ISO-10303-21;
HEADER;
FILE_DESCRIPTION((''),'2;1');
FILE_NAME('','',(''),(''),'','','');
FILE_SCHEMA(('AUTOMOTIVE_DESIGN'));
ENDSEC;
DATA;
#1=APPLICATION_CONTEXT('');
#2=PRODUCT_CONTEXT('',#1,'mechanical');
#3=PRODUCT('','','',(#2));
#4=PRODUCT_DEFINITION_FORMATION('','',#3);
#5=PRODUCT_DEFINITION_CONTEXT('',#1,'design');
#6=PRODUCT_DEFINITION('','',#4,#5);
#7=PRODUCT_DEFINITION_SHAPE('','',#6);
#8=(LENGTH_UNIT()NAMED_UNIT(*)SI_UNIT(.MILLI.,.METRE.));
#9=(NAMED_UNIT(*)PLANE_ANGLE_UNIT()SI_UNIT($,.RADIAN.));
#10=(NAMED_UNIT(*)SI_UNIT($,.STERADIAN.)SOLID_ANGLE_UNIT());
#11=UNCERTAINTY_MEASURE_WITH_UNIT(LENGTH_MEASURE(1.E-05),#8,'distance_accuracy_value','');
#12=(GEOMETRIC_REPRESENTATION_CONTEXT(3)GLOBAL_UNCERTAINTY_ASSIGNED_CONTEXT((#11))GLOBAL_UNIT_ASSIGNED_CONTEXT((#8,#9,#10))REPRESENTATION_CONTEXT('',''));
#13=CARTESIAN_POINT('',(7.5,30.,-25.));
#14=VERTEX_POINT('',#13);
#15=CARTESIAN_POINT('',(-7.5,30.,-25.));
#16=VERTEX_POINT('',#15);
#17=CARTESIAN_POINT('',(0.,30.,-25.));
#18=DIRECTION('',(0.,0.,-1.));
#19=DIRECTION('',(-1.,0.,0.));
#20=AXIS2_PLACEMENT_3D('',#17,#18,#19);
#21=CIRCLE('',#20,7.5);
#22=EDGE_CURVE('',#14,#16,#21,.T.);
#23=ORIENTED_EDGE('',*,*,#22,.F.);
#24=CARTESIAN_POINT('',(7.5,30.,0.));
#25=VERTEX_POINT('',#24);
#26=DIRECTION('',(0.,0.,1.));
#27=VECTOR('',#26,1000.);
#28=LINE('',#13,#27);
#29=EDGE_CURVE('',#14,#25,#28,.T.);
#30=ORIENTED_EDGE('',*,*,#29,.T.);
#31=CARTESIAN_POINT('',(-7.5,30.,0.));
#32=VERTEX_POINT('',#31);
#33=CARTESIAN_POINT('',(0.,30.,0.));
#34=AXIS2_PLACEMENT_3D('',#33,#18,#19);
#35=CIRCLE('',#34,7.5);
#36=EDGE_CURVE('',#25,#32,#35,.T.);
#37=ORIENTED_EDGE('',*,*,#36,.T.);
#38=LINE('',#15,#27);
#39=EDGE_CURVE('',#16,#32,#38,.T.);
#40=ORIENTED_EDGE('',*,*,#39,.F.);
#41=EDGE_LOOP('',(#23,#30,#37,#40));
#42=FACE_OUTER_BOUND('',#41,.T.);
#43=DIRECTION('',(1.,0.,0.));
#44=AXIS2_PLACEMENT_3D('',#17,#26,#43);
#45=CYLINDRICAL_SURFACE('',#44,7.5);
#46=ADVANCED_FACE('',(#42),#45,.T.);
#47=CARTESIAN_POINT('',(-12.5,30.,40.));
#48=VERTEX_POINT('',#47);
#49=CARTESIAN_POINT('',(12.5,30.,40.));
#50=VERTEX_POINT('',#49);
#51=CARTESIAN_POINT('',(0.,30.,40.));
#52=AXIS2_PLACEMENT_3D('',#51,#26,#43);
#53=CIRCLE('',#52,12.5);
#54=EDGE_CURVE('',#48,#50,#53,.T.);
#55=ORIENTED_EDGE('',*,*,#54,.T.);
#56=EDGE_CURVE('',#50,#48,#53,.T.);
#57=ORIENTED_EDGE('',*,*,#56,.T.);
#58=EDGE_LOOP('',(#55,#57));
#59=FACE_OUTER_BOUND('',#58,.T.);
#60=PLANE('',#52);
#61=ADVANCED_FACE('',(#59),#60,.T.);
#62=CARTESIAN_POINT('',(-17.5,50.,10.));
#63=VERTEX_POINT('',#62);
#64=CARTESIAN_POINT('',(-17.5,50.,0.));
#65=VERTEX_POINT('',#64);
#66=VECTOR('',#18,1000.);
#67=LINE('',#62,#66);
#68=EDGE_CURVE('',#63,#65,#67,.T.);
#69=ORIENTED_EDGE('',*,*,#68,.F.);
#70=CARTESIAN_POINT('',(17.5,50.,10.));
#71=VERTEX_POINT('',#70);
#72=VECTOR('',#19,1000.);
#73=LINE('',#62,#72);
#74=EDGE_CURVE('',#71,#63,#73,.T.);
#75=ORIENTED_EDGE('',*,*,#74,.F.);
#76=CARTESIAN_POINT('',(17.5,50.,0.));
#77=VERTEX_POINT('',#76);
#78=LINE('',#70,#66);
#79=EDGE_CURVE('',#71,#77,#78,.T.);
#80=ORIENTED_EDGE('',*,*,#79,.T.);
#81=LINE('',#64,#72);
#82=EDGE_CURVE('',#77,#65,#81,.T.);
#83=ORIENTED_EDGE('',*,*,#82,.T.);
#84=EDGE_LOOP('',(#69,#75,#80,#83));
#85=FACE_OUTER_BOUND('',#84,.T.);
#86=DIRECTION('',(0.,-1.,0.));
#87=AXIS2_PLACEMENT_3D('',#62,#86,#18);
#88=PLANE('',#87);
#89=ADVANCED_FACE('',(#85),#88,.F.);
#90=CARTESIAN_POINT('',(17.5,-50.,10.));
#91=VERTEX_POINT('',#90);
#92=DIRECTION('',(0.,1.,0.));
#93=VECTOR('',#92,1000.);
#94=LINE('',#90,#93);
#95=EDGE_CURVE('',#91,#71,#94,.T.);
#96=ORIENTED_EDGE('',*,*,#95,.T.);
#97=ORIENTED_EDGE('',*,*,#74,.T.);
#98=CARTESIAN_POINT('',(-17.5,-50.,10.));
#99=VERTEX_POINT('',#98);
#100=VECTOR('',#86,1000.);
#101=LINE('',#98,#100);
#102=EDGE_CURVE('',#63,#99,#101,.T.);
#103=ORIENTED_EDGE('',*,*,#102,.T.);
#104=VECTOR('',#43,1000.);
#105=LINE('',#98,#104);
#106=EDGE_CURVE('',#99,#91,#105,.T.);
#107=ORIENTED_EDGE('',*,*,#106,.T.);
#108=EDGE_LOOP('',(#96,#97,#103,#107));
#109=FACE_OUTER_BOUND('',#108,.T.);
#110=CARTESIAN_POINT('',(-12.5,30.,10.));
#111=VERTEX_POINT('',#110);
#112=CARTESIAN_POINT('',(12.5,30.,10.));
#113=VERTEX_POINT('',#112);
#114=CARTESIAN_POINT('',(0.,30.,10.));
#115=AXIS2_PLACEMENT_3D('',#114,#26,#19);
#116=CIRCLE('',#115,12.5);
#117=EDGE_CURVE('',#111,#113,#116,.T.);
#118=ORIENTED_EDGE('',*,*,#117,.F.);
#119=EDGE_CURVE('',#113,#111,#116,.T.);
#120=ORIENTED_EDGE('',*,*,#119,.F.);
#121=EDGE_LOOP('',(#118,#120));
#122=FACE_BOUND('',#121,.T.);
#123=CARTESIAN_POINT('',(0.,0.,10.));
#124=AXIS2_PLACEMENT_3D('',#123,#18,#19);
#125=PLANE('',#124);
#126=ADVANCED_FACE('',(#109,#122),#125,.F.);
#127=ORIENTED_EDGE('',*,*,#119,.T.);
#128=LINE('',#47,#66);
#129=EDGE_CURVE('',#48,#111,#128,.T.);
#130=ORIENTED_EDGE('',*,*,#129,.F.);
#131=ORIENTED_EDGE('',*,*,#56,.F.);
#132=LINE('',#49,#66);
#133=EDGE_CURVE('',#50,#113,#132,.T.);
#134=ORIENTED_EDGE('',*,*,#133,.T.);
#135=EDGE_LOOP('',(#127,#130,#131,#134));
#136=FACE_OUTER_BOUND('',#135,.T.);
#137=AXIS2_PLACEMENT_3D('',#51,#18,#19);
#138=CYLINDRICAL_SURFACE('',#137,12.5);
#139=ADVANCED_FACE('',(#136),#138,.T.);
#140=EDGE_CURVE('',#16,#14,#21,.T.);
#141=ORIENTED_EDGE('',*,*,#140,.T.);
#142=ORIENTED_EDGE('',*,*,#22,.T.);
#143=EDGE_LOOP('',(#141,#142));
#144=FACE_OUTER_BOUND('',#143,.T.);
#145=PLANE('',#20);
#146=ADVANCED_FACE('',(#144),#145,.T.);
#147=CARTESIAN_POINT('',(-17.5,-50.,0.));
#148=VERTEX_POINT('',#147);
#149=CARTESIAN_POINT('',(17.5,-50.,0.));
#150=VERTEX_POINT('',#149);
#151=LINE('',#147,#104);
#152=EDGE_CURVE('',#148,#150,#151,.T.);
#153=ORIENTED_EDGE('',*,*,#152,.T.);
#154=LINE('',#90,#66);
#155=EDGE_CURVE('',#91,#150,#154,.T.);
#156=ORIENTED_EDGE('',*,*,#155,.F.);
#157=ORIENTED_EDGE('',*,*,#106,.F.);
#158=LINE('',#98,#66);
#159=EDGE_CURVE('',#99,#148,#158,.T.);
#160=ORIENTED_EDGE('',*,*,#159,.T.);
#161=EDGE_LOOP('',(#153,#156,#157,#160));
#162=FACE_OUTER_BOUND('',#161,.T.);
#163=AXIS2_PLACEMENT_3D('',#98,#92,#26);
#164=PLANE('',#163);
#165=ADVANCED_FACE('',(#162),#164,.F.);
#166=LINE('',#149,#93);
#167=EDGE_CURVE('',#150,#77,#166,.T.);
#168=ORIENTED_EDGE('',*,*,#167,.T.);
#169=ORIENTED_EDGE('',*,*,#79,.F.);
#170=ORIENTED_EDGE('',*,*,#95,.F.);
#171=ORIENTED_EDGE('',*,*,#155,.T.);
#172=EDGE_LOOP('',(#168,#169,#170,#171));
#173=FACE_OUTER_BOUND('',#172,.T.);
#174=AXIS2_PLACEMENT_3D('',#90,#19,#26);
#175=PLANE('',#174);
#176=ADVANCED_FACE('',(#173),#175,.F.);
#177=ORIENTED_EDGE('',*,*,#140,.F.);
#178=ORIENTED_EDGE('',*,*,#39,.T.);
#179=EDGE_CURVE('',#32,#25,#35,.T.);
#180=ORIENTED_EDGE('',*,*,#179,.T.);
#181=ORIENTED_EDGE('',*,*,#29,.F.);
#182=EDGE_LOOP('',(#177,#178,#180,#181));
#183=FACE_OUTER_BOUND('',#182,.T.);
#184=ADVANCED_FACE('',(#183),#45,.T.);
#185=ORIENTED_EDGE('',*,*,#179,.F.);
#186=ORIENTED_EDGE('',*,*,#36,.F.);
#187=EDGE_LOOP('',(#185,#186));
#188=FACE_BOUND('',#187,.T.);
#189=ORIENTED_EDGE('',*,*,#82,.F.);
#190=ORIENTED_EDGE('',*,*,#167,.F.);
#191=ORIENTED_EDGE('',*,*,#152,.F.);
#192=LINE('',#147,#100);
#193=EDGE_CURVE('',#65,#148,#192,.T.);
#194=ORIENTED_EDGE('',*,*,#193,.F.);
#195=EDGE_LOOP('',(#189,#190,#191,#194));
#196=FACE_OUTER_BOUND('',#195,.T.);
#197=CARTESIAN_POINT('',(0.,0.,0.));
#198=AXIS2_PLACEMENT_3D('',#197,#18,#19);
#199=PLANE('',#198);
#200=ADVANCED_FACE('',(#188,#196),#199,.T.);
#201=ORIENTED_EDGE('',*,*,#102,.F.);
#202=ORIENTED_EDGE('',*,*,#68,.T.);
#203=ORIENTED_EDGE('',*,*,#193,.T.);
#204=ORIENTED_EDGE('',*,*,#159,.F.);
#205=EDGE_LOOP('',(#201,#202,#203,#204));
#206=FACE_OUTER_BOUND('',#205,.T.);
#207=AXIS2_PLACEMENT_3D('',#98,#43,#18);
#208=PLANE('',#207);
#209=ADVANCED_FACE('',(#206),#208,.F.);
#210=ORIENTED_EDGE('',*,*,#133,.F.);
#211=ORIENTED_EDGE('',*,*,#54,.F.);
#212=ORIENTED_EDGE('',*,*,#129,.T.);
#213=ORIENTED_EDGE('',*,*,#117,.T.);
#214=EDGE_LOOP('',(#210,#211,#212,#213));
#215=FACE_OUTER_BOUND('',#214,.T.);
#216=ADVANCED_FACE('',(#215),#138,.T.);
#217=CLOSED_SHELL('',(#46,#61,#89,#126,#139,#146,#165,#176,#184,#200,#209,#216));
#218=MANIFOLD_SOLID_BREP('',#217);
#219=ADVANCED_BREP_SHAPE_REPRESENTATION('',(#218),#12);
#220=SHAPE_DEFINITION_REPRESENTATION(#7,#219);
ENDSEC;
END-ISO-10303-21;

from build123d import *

# Parameters (mm, degrees)
SKETCH_1_W      = 35
SKETCH_1_H      = 100
EXTRUDE_1_DEPTH = 10
SKETCH_2_R      = 12.5
EXTRUDE_2_DEPTH = 30
SKETCH_3_R      = 7.5
EXTRUDE_3_DEPTH = 25


with BuildPart() as part:
    # 草图1 → 凸台-拉伸1 (new body)
    with BuildSketch(Plane.XY):
        Rectangle(SKETCH_1_W, SKETCH_1_H)
    extrude(amount=EXTRUDE_1_DEPTH)

    # 草图2 → 凸台-拉伸2 (add)
    with BuildSketch(Plane.XY.offset(10)):
        with Locations(Location((0, 30, 0), (0, 0, 180))):
            Circle(SKETCH_2_R)
    extrude(amount=EXTRUDE_2_DEPTH)

    # 草图3 → 凸台-拉伸3 (add)
    with BuildSketch(Plane(origin=(0, 0, 0), x_dir=(-1, 0, 0), z_dir=(0, 0, -1))):
        with Locations((0, 30)):
            Circle(SKETCH_3_R)
    extrude(amount=EXTRUDE_3_DEPTH)


solid = part.part
